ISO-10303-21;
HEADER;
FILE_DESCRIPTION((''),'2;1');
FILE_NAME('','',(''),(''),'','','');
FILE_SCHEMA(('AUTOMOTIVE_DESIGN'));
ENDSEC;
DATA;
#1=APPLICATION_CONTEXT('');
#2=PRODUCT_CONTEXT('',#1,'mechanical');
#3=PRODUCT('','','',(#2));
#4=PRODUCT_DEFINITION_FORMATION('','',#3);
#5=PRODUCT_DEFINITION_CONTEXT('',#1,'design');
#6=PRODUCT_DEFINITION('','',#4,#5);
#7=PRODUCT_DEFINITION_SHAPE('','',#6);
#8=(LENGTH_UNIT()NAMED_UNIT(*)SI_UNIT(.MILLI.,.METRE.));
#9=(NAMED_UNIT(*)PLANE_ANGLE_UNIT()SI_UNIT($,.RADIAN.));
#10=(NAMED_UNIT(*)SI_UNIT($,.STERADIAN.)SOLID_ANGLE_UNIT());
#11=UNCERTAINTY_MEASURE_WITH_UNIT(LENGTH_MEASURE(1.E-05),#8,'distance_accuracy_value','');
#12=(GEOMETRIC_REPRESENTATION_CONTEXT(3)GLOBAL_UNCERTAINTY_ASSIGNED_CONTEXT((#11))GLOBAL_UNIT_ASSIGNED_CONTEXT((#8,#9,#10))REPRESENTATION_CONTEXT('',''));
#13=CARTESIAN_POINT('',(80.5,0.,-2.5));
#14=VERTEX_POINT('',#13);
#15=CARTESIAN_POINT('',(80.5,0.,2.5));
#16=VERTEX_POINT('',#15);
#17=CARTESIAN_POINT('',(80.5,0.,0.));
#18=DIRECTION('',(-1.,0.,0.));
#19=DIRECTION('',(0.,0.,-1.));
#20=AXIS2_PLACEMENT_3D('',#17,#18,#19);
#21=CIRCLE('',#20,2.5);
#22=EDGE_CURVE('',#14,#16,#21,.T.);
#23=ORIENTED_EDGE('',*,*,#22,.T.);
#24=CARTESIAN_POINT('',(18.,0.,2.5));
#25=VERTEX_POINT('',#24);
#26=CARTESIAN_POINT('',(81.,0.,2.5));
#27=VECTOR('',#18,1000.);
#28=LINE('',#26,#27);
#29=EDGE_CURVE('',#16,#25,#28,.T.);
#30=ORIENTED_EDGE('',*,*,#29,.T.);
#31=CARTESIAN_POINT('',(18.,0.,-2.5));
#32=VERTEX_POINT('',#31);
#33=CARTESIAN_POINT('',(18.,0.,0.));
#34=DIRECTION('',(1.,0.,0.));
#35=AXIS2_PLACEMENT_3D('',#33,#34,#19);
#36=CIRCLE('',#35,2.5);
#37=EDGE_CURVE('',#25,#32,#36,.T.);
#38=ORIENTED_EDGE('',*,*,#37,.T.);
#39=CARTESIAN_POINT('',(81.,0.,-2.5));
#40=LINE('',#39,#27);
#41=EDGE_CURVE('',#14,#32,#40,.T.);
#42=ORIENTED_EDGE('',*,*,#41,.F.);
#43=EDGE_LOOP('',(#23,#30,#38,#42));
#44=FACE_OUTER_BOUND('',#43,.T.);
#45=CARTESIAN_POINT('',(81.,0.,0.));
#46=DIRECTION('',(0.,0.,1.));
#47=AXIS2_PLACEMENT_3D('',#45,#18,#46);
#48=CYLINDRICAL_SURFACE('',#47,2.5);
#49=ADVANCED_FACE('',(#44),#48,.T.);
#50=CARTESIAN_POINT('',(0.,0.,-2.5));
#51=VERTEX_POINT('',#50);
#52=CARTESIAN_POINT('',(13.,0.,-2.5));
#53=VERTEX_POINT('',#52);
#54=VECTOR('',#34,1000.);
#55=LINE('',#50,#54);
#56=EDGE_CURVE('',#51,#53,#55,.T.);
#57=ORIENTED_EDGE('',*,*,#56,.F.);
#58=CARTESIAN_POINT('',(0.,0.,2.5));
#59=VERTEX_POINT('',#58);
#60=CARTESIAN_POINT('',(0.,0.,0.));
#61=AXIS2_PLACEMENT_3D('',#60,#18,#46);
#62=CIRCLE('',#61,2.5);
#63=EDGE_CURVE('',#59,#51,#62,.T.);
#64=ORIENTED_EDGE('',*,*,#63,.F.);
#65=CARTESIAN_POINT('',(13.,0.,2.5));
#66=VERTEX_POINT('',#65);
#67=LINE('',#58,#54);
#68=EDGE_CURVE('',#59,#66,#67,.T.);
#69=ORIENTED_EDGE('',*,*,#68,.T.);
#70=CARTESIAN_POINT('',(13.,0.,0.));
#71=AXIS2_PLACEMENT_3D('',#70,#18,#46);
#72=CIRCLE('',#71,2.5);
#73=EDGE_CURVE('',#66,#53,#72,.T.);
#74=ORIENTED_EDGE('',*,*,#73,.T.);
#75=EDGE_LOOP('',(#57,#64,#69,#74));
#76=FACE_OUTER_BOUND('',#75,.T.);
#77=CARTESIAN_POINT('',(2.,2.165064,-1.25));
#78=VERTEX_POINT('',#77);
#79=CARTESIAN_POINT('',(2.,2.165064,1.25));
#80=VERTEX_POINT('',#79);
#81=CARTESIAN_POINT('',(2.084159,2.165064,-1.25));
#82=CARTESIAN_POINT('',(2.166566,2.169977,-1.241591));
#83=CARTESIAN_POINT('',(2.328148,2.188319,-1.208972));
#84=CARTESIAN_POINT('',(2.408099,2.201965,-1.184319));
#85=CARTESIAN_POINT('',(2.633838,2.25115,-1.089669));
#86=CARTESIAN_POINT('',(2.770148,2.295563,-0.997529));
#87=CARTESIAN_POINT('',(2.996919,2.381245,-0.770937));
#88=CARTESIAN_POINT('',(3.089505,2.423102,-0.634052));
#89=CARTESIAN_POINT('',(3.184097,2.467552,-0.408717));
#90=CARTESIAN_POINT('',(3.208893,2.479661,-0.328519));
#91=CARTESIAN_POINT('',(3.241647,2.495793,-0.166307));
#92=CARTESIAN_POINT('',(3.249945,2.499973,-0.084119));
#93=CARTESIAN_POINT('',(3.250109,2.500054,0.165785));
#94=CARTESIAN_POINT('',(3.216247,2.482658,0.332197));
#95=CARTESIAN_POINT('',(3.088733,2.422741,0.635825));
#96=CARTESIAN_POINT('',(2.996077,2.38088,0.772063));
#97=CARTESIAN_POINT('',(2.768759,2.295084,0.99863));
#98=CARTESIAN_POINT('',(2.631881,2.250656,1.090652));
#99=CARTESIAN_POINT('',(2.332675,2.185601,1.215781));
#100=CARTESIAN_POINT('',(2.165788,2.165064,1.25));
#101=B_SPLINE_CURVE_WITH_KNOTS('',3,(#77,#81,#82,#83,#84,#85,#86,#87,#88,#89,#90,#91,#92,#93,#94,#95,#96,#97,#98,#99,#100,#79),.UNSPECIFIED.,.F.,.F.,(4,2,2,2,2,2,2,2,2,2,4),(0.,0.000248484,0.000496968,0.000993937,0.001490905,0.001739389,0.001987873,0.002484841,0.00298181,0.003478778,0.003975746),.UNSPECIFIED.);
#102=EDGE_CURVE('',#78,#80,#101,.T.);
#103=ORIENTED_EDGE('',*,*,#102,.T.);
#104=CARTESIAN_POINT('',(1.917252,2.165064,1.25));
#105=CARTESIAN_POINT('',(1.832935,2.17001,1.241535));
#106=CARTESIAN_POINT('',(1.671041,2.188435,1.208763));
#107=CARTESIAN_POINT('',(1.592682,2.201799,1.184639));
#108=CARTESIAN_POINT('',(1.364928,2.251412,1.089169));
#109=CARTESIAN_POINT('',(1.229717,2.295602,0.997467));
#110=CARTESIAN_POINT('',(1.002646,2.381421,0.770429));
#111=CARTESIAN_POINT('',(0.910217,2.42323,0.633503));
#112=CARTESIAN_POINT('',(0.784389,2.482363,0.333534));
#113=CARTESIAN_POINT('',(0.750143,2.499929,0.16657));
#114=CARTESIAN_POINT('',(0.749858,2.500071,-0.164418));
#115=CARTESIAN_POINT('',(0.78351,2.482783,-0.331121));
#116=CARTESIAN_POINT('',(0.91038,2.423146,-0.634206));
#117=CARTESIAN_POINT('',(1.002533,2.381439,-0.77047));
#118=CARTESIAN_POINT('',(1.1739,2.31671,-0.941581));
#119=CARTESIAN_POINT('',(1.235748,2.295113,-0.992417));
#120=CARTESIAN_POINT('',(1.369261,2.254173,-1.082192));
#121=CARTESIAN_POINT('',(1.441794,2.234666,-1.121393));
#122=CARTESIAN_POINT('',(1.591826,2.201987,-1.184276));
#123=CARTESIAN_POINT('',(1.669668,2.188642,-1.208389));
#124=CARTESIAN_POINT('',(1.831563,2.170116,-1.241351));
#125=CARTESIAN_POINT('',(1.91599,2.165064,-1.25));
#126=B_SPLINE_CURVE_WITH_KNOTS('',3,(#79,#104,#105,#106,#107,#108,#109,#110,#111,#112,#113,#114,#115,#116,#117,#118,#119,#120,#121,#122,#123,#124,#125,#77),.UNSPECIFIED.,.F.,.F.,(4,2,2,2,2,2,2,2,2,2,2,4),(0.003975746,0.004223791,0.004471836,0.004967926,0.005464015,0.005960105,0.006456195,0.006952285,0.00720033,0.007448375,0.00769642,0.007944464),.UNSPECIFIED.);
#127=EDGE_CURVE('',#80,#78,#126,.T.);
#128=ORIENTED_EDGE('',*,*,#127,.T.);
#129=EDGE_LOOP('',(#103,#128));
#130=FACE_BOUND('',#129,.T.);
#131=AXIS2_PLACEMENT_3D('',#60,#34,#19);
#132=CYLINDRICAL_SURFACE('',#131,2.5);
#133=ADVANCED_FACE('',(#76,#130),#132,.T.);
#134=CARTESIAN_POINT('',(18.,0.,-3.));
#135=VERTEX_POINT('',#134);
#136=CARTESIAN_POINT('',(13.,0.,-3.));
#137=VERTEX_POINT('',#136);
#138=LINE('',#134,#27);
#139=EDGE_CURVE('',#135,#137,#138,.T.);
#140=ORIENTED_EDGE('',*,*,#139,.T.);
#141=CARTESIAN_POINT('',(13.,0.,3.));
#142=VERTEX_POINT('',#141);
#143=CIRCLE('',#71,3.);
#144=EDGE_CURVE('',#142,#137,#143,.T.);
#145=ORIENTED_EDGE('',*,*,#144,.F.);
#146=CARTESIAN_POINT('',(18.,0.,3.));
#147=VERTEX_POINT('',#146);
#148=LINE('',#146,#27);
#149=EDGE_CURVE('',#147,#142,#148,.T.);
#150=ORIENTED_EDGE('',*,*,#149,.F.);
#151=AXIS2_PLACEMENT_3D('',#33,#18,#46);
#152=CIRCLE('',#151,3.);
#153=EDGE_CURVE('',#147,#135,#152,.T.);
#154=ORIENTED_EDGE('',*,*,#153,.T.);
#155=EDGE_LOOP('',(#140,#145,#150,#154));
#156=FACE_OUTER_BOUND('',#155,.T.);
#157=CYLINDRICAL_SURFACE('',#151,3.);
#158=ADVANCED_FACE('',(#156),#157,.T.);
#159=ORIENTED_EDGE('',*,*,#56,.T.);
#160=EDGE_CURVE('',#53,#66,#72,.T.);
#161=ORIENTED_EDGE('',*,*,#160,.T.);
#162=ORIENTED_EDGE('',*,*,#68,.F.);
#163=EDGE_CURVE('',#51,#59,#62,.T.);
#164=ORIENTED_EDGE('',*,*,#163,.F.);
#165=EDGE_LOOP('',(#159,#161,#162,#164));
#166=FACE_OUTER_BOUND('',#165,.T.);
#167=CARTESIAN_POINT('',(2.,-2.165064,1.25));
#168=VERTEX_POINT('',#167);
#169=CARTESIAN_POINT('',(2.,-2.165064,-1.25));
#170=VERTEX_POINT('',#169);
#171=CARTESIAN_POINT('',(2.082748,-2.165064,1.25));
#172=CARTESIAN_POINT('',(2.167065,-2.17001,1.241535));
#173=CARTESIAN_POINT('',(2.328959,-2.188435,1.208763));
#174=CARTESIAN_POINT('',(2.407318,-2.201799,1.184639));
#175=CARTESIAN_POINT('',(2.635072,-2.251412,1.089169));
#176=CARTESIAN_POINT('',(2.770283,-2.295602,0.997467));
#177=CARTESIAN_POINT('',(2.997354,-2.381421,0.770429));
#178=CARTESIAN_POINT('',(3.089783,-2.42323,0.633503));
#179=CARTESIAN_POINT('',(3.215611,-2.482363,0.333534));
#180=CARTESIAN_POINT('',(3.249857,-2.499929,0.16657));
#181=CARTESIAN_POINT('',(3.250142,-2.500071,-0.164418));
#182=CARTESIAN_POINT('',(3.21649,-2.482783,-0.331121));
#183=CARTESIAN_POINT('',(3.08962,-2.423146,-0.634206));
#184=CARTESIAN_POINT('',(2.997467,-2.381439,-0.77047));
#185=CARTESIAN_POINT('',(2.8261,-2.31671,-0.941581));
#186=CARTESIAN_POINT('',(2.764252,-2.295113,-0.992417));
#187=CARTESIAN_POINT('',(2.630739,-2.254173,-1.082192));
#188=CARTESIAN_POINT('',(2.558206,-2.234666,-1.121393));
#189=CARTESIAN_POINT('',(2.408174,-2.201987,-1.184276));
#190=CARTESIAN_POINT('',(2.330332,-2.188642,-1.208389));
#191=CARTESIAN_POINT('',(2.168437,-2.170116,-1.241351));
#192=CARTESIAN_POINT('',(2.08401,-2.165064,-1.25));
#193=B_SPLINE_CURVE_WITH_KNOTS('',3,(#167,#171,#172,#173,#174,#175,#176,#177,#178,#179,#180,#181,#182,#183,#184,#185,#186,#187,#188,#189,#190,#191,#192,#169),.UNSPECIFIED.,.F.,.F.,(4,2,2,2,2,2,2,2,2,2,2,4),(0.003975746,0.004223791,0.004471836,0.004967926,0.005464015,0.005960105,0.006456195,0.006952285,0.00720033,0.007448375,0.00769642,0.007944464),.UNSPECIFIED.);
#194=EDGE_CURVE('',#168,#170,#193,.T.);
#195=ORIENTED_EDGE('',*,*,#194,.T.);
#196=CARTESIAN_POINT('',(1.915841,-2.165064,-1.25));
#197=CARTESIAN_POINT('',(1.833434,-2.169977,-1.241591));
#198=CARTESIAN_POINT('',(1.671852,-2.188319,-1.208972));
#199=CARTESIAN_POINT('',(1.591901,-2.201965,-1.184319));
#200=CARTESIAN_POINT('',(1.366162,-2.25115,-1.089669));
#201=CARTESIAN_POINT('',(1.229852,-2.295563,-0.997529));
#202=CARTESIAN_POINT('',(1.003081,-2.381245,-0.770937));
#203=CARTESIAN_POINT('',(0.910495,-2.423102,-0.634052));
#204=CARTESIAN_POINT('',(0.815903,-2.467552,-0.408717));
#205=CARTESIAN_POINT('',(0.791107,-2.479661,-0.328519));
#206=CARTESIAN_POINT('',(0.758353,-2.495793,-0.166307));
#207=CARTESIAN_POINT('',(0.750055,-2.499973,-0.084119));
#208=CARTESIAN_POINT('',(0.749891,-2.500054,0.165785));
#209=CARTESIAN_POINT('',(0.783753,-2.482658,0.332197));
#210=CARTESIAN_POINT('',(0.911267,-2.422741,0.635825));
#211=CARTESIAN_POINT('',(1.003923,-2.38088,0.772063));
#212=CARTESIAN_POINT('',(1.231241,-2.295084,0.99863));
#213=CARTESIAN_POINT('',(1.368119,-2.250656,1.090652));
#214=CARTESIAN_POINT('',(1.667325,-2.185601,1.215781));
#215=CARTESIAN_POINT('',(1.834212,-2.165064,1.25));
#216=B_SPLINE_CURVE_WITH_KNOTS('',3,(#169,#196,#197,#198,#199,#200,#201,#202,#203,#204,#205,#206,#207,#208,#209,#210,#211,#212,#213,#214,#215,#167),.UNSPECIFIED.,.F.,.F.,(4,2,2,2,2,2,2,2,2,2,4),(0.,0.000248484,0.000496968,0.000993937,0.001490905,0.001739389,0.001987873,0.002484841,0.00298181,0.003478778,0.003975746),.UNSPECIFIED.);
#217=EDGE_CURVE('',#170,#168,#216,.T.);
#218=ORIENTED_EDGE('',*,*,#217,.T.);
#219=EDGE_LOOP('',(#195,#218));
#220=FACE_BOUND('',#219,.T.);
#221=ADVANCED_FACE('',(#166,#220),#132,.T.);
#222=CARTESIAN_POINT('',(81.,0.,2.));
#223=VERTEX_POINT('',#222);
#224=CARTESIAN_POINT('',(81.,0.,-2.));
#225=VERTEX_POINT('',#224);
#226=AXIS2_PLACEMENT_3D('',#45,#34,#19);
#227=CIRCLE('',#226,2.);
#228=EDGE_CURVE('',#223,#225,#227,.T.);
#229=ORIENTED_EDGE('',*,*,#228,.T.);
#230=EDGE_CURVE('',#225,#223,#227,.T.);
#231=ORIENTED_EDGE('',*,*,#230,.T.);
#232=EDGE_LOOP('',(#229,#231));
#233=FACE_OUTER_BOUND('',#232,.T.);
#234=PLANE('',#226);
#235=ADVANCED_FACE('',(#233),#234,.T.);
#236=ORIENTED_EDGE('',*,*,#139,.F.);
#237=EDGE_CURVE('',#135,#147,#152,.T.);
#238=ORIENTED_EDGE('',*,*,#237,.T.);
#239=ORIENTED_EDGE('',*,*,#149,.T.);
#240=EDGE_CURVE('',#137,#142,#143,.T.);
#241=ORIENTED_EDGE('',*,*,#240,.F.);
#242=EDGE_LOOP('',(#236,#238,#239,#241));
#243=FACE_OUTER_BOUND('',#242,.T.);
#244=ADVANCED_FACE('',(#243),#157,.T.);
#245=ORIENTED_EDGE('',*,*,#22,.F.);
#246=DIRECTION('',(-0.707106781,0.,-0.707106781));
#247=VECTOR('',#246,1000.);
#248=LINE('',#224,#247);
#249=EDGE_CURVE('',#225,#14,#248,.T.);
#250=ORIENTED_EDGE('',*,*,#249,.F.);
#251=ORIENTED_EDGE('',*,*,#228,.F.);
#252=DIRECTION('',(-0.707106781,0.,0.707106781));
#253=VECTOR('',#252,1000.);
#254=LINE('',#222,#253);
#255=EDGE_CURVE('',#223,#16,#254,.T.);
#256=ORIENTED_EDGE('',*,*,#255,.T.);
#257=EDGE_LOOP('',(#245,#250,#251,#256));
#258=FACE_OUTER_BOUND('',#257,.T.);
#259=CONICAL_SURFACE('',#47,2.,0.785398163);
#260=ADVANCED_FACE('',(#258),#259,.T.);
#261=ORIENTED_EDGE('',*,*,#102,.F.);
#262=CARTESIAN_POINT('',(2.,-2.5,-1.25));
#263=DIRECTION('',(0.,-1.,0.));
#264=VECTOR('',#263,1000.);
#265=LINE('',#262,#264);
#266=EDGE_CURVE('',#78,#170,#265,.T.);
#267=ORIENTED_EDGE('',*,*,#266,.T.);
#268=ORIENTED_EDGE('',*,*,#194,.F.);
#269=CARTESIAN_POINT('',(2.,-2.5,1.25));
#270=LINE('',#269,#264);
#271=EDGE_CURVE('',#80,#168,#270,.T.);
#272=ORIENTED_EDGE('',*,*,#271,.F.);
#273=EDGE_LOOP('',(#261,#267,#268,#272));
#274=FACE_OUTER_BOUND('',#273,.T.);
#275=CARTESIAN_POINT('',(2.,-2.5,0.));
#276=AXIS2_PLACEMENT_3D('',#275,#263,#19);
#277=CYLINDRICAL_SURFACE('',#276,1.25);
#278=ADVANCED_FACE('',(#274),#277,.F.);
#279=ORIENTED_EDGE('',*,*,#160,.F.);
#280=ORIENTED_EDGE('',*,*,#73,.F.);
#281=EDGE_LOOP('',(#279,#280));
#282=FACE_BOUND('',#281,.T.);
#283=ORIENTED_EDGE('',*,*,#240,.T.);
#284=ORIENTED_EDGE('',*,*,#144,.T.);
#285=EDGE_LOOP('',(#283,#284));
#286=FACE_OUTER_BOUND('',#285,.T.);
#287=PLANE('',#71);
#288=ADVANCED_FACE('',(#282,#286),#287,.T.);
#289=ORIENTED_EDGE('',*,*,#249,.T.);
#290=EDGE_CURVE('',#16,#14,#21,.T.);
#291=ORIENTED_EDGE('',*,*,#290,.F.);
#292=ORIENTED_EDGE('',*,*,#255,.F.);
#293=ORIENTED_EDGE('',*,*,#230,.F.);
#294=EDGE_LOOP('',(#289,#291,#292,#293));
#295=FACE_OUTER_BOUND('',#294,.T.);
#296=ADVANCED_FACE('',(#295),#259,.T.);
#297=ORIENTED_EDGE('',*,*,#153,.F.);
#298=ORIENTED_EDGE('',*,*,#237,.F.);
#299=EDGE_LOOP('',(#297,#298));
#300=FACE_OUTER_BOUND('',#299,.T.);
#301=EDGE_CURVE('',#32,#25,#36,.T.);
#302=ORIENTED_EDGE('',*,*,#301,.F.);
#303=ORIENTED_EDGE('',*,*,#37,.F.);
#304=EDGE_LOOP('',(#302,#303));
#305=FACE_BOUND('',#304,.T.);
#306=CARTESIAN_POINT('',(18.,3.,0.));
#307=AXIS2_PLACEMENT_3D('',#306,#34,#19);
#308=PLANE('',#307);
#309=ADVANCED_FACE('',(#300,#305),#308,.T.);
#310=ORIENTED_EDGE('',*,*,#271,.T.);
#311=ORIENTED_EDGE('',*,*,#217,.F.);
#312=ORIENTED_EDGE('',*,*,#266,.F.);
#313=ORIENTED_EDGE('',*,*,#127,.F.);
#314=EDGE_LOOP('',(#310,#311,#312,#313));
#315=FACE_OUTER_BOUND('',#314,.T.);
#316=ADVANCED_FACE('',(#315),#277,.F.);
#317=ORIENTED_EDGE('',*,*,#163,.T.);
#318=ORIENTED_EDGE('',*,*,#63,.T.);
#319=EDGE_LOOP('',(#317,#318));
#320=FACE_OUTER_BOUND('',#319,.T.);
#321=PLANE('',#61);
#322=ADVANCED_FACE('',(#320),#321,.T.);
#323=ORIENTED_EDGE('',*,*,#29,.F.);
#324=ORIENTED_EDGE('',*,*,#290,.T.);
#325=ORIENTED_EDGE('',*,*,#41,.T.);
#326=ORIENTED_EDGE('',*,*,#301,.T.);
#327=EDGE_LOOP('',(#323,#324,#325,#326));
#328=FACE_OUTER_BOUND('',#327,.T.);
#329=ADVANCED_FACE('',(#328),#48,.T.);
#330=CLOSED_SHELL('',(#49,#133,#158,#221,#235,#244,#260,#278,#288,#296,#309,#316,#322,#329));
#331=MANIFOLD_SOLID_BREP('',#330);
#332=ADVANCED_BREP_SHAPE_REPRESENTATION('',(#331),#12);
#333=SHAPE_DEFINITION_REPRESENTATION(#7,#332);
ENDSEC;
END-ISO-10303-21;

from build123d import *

# Parameters (mm, degrees)
SKETCH1_W                      = 5
SKETCH1_H                      = 3
SKETCH2_R                      = 2.5
BOSS_EXTRUDE1_DEPTH            = 13
BOSS_EXTRUDE2_START            = 63
SKETCH3_R                      = 2.5
BOSS_EXTRUDE2_DEPTH            = 63
F_2_5_2_5_DIAMETER_HOLE1_D     = 2.5
F_2_5_2_5_DIAMETER_HOLE1_DEPTH = 5.5
CHAMFER1_SIZE                  = 0.5


with BuildPart() as part:
    # Sketch1 → Revolve1 (revolve)
    with BuildSketch(Plane(origin=(0, 0, 0), x_dir=(-1, 0, 0), z_dir=(0, 0, -1)), mode=Mode.PRIVATE) as revolve1_sk:
        with Locations((-15.5, 1.5)):
            Rectangle(SKETCH1_W, SKETCH1_H)
    revolve(revolve1_sk.sketch.rotate(Axis((18, 0, 0), (-1, 0, 0)), 270), axis=Axis((18, 0, 0), (-1, 0, 0)))

    # Sketch2 → Boss-Extrude1 (add)
    with BuildSketch(Plane.ZY.offset(-13)):
        with Locations(Location((0, 0, 0), (0, 0, 180))):
            Circle(SKETCH2_R)
    extrude(amount=BOSS_EXTRUDE1_DEPTH)

    # Sketch3 → Boss-Extrude2 (add)
    with BuildSketch(Plane(origin=(18, 0, 0), x_dir=(0, 0, -1), z_dir=(1, 0, 0)).offset(BOSS_EXTRUDE2_START)):
        Circle(SKETCH3_R)
    extrude(amount=-BOSS_EXTRUDE2_DEPTH)

    # Ø2.5 (2.5) Diameter Hole1
    with Locations(Plane(origin=(2, -2.5, 0), x_dir=(-1, 0, 0), z_dir=(0, -1, 0))):
        with Locations((0, 0)):
            Hole(F_2_5_2_5_DIAMETER_HOLE1_D / 2, depth=F_2_5_2_5_DIAMETER_HOLE1_DEPTH)

    # Chamfer1
    chamfer1_edges = [part.edges().sort_by_distance(p)[0] for p in [
        (81, 0, 2.5),
    ]]
    chamfer(chamfer1_edges, length=CHAMFER1_SIZE)


solid = part.part
